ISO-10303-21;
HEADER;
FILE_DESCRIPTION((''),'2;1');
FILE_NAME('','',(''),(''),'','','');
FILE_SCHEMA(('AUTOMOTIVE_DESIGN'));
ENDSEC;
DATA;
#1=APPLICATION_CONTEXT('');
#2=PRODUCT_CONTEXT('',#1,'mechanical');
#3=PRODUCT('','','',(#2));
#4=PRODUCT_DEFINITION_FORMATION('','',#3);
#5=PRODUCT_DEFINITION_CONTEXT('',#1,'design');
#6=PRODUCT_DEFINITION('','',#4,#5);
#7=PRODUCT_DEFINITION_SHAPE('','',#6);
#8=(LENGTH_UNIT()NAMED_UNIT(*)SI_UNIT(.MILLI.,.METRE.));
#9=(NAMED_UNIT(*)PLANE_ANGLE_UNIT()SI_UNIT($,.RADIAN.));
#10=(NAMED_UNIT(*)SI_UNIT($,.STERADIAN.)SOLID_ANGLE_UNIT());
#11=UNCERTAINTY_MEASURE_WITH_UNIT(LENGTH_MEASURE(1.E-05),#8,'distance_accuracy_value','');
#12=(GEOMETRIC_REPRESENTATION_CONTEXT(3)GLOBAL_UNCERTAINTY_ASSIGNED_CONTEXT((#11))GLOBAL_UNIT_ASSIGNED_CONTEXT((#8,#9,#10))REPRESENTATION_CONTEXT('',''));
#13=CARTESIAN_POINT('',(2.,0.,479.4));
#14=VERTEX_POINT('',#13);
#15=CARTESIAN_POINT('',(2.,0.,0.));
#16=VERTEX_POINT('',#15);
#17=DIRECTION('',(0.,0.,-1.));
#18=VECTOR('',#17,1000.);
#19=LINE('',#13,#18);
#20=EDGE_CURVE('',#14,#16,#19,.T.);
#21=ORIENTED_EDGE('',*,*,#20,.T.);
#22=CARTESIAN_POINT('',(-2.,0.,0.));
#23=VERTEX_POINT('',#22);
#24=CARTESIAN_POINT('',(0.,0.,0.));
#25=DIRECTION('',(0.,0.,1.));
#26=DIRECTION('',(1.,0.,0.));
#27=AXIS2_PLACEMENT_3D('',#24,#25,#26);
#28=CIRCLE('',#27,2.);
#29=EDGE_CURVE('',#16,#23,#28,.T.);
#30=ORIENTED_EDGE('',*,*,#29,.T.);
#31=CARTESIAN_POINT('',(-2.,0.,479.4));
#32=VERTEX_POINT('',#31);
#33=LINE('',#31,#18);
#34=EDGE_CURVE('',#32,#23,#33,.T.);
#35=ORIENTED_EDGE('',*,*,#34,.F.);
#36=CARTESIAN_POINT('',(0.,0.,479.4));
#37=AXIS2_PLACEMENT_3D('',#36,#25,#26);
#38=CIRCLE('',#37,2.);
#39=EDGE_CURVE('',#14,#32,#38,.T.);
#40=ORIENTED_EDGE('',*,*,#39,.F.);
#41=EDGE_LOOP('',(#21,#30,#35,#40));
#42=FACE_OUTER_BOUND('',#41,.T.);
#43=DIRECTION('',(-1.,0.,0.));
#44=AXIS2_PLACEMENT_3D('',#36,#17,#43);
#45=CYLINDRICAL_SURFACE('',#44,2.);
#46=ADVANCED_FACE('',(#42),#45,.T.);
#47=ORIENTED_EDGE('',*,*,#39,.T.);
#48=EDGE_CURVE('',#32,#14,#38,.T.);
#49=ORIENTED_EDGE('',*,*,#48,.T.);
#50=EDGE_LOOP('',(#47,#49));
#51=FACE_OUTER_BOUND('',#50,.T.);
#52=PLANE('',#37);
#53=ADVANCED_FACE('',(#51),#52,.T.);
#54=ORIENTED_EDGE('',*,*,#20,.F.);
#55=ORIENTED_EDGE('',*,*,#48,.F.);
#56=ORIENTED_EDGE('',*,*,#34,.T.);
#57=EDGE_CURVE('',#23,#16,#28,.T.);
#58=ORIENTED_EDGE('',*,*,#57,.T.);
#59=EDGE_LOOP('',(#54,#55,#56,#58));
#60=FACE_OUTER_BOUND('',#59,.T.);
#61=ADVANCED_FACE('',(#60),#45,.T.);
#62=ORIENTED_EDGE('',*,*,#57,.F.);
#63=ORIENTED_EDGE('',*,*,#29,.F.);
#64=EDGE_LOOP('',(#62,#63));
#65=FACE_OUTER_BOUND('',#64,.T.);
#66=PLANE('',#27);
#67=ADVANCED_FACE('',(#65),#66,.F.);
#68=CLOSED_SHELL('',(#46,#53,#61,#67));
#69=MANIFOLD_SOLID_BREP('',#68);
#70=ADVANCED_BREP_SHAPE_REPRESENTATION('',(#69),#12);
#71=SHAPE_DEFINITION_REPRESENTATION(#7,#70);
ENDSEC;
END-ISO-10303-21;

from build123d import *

# Parameters (mm, degrees)
SKETCH1_R           = 2
BOSS_EXTRUDE1_DEPTH = 479.4


with BuildPart() as part:
    # Sketch1 → Boss-Extrude1 (new body)
    with BuildSketch(Plane.XY):
        Circle(SKETCH1_R)
    extrude(amount=BOSS_EXTRUDE1_DEPTH)


solid = part.part
